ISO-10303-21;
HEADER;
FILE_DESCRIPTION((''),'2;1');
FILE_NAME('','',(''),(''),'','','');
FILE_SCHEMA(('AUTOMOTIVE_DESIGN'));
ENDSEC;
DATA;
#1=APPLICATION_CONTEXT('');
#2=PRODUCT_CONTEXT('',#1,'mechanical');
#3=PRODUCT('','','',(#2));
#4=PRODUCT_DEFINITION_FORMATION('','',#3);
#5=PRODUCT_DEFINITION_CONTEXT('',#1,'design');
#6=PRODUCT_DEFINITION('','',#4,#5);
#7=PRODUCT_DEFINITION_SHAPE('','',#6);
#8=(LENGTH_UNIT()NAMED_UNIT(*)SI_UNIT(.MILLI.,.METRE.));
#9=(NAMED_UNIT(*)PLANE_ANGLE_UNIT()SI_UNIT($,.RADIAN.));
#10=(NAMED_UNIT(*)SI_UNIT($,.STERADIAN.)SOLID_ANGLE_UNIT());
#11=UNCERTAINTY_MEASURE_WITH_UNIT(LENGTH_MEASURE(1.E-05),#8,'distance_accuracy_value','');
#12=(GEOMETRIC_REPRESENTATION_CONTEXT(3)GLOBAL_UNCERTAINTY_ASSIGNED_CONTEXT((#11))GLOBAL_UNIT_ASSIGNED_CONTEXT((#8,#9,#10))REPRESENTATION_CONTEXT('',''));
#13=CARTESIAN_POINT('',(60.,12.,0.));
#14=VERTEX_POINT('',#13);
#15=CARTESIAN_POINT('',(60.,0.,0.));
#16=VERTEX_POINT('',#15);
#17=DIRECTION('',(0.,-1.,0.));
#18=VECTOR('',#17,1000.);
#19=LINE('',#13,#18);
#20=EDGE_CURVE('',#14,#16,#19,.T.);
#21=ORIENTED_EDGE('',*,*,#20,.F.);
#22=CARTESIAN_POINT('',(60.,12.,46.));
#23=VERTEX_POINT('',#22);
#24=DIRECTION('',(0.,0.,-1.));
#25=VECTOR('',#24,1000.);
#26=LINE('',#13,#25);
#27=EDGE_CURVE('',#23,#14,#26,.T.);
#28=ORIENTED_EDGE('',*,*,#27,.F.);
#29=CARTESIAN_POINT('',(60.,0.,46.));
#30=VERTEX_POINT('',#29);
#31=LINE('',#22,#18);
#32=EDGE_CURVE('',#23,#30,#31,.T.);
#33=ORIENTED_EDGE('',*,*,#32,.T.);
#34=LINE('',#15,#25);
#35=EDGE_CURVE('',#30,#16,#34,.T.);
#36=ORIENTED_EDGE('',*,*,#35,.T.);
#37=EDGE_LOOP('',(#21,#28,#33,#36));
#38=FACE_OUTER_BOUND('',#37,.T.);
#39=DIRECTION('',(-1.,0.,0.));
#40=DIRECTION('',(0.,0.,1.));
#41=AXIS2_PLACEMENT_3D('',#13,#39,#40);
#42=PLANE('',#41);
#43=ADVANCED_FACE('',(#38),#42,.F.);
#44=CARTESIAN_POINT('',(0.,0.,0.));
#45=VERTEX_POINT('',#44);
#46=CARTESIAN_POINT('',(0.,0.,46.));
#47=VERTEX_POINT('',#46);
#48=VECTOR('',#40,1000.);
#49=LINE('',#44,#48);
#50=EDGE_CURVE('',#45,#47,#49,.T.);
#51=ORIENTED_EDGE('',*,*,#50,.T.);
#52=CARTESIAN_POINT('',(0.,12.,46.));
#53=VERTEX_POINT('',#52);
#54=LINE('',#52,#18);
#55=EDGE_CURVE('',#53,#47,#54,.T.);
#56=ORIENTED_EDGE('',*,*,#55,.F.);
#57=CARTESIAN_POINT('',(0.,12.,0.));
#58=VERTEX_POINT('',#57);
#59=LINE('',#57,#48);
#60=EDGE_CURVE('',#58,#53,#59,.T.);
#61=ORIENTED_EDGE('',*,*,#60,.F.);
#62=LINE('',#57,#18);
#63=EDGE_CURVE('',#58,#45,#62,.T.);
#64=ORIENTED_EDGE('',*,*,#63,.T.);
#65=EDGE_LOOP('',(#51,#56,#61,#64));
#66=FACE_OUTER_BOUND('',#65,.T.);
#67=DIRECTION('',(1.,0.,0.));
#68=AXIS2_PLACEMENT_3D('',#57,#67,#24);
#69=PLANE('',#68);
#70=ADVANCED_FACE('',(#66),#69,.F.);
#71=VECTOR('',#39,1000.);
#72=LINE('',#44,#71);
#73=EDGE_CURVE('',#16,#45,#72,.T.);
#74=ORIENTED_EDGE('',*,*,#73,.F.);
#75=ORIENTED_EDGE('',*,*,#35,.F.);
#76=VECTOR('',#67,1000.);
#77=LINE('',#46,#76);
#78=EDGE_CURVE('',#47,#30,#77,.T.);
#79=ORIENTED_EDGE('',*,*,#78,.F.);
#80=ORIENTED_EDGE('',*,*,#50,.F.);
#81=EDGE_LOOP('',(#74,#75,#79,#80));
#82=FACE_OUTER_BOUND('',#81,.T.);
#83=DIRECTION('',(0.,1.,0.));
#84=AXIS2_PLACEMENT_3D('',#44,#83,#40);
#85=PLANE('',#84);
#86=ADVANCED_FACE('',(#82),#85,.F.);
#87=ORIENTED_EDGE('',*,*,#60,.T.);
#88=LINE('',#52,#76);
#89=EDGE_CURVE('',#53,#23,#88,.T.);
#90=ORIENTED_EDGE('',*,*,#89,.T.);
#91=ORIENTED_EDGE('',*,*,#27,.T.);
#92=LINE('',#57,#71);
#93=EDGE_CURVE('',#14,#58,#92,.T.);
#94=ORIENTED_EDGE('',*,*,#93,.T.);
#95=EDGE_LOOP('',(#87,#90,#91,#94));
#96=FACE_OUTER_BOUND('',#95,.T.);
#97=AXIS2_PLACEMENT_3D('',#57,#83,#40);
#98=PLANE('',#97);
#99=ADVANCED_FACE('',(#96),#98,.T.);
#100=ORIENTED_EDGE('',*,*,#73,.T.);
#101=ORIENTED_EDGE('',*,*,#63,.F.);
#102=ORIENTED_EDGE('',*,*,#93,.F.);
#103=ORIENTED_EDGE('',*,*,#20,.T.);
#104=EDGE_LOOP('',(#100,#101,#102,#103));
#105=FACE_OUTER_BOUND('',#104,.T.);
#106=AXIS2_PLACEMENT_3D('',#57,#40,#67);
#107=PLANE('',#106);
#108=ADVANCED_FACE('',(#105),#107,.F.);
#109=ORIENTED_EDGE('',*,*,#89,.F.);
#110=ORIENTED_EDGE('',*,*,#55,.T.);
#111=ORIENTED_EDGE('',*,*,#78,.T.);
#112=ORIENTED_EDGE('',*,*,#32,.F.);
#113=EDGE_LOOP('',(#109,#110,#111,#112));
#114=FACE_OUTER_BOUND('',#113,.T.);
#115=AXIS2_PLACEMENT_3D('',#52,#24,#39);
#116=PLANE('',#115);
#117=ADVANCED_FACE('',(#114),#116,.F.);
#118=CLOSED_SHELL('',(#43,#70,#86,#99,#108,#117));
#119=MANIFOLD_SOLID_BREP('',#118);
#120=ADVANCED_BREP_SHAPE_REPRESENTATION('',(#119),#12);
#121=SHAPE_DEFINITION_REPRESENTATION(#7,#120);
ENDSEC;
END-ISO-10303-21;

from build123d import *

# Parameters (mm, degrees)
SKETCH1_W           = 60
SKETCH1_H           = 46
BOSS_EXTRUDE1_DEPTH = 12


with BuildPart() as part:
    # Sketch1 → Boss-Extrude1 (new body)
    with BuildSketch(Plane(origin=(0, 0, 0), x_dir=(1, 0, 0), z_dir=(0, 1, 0))):
        with Locations((30, -23)):
            Rectangle(SKETCH1_W, SKETCH1_H)
    extrude(amount=BOSS_EXTRUDE1_DEPTH)


solid = part.part
